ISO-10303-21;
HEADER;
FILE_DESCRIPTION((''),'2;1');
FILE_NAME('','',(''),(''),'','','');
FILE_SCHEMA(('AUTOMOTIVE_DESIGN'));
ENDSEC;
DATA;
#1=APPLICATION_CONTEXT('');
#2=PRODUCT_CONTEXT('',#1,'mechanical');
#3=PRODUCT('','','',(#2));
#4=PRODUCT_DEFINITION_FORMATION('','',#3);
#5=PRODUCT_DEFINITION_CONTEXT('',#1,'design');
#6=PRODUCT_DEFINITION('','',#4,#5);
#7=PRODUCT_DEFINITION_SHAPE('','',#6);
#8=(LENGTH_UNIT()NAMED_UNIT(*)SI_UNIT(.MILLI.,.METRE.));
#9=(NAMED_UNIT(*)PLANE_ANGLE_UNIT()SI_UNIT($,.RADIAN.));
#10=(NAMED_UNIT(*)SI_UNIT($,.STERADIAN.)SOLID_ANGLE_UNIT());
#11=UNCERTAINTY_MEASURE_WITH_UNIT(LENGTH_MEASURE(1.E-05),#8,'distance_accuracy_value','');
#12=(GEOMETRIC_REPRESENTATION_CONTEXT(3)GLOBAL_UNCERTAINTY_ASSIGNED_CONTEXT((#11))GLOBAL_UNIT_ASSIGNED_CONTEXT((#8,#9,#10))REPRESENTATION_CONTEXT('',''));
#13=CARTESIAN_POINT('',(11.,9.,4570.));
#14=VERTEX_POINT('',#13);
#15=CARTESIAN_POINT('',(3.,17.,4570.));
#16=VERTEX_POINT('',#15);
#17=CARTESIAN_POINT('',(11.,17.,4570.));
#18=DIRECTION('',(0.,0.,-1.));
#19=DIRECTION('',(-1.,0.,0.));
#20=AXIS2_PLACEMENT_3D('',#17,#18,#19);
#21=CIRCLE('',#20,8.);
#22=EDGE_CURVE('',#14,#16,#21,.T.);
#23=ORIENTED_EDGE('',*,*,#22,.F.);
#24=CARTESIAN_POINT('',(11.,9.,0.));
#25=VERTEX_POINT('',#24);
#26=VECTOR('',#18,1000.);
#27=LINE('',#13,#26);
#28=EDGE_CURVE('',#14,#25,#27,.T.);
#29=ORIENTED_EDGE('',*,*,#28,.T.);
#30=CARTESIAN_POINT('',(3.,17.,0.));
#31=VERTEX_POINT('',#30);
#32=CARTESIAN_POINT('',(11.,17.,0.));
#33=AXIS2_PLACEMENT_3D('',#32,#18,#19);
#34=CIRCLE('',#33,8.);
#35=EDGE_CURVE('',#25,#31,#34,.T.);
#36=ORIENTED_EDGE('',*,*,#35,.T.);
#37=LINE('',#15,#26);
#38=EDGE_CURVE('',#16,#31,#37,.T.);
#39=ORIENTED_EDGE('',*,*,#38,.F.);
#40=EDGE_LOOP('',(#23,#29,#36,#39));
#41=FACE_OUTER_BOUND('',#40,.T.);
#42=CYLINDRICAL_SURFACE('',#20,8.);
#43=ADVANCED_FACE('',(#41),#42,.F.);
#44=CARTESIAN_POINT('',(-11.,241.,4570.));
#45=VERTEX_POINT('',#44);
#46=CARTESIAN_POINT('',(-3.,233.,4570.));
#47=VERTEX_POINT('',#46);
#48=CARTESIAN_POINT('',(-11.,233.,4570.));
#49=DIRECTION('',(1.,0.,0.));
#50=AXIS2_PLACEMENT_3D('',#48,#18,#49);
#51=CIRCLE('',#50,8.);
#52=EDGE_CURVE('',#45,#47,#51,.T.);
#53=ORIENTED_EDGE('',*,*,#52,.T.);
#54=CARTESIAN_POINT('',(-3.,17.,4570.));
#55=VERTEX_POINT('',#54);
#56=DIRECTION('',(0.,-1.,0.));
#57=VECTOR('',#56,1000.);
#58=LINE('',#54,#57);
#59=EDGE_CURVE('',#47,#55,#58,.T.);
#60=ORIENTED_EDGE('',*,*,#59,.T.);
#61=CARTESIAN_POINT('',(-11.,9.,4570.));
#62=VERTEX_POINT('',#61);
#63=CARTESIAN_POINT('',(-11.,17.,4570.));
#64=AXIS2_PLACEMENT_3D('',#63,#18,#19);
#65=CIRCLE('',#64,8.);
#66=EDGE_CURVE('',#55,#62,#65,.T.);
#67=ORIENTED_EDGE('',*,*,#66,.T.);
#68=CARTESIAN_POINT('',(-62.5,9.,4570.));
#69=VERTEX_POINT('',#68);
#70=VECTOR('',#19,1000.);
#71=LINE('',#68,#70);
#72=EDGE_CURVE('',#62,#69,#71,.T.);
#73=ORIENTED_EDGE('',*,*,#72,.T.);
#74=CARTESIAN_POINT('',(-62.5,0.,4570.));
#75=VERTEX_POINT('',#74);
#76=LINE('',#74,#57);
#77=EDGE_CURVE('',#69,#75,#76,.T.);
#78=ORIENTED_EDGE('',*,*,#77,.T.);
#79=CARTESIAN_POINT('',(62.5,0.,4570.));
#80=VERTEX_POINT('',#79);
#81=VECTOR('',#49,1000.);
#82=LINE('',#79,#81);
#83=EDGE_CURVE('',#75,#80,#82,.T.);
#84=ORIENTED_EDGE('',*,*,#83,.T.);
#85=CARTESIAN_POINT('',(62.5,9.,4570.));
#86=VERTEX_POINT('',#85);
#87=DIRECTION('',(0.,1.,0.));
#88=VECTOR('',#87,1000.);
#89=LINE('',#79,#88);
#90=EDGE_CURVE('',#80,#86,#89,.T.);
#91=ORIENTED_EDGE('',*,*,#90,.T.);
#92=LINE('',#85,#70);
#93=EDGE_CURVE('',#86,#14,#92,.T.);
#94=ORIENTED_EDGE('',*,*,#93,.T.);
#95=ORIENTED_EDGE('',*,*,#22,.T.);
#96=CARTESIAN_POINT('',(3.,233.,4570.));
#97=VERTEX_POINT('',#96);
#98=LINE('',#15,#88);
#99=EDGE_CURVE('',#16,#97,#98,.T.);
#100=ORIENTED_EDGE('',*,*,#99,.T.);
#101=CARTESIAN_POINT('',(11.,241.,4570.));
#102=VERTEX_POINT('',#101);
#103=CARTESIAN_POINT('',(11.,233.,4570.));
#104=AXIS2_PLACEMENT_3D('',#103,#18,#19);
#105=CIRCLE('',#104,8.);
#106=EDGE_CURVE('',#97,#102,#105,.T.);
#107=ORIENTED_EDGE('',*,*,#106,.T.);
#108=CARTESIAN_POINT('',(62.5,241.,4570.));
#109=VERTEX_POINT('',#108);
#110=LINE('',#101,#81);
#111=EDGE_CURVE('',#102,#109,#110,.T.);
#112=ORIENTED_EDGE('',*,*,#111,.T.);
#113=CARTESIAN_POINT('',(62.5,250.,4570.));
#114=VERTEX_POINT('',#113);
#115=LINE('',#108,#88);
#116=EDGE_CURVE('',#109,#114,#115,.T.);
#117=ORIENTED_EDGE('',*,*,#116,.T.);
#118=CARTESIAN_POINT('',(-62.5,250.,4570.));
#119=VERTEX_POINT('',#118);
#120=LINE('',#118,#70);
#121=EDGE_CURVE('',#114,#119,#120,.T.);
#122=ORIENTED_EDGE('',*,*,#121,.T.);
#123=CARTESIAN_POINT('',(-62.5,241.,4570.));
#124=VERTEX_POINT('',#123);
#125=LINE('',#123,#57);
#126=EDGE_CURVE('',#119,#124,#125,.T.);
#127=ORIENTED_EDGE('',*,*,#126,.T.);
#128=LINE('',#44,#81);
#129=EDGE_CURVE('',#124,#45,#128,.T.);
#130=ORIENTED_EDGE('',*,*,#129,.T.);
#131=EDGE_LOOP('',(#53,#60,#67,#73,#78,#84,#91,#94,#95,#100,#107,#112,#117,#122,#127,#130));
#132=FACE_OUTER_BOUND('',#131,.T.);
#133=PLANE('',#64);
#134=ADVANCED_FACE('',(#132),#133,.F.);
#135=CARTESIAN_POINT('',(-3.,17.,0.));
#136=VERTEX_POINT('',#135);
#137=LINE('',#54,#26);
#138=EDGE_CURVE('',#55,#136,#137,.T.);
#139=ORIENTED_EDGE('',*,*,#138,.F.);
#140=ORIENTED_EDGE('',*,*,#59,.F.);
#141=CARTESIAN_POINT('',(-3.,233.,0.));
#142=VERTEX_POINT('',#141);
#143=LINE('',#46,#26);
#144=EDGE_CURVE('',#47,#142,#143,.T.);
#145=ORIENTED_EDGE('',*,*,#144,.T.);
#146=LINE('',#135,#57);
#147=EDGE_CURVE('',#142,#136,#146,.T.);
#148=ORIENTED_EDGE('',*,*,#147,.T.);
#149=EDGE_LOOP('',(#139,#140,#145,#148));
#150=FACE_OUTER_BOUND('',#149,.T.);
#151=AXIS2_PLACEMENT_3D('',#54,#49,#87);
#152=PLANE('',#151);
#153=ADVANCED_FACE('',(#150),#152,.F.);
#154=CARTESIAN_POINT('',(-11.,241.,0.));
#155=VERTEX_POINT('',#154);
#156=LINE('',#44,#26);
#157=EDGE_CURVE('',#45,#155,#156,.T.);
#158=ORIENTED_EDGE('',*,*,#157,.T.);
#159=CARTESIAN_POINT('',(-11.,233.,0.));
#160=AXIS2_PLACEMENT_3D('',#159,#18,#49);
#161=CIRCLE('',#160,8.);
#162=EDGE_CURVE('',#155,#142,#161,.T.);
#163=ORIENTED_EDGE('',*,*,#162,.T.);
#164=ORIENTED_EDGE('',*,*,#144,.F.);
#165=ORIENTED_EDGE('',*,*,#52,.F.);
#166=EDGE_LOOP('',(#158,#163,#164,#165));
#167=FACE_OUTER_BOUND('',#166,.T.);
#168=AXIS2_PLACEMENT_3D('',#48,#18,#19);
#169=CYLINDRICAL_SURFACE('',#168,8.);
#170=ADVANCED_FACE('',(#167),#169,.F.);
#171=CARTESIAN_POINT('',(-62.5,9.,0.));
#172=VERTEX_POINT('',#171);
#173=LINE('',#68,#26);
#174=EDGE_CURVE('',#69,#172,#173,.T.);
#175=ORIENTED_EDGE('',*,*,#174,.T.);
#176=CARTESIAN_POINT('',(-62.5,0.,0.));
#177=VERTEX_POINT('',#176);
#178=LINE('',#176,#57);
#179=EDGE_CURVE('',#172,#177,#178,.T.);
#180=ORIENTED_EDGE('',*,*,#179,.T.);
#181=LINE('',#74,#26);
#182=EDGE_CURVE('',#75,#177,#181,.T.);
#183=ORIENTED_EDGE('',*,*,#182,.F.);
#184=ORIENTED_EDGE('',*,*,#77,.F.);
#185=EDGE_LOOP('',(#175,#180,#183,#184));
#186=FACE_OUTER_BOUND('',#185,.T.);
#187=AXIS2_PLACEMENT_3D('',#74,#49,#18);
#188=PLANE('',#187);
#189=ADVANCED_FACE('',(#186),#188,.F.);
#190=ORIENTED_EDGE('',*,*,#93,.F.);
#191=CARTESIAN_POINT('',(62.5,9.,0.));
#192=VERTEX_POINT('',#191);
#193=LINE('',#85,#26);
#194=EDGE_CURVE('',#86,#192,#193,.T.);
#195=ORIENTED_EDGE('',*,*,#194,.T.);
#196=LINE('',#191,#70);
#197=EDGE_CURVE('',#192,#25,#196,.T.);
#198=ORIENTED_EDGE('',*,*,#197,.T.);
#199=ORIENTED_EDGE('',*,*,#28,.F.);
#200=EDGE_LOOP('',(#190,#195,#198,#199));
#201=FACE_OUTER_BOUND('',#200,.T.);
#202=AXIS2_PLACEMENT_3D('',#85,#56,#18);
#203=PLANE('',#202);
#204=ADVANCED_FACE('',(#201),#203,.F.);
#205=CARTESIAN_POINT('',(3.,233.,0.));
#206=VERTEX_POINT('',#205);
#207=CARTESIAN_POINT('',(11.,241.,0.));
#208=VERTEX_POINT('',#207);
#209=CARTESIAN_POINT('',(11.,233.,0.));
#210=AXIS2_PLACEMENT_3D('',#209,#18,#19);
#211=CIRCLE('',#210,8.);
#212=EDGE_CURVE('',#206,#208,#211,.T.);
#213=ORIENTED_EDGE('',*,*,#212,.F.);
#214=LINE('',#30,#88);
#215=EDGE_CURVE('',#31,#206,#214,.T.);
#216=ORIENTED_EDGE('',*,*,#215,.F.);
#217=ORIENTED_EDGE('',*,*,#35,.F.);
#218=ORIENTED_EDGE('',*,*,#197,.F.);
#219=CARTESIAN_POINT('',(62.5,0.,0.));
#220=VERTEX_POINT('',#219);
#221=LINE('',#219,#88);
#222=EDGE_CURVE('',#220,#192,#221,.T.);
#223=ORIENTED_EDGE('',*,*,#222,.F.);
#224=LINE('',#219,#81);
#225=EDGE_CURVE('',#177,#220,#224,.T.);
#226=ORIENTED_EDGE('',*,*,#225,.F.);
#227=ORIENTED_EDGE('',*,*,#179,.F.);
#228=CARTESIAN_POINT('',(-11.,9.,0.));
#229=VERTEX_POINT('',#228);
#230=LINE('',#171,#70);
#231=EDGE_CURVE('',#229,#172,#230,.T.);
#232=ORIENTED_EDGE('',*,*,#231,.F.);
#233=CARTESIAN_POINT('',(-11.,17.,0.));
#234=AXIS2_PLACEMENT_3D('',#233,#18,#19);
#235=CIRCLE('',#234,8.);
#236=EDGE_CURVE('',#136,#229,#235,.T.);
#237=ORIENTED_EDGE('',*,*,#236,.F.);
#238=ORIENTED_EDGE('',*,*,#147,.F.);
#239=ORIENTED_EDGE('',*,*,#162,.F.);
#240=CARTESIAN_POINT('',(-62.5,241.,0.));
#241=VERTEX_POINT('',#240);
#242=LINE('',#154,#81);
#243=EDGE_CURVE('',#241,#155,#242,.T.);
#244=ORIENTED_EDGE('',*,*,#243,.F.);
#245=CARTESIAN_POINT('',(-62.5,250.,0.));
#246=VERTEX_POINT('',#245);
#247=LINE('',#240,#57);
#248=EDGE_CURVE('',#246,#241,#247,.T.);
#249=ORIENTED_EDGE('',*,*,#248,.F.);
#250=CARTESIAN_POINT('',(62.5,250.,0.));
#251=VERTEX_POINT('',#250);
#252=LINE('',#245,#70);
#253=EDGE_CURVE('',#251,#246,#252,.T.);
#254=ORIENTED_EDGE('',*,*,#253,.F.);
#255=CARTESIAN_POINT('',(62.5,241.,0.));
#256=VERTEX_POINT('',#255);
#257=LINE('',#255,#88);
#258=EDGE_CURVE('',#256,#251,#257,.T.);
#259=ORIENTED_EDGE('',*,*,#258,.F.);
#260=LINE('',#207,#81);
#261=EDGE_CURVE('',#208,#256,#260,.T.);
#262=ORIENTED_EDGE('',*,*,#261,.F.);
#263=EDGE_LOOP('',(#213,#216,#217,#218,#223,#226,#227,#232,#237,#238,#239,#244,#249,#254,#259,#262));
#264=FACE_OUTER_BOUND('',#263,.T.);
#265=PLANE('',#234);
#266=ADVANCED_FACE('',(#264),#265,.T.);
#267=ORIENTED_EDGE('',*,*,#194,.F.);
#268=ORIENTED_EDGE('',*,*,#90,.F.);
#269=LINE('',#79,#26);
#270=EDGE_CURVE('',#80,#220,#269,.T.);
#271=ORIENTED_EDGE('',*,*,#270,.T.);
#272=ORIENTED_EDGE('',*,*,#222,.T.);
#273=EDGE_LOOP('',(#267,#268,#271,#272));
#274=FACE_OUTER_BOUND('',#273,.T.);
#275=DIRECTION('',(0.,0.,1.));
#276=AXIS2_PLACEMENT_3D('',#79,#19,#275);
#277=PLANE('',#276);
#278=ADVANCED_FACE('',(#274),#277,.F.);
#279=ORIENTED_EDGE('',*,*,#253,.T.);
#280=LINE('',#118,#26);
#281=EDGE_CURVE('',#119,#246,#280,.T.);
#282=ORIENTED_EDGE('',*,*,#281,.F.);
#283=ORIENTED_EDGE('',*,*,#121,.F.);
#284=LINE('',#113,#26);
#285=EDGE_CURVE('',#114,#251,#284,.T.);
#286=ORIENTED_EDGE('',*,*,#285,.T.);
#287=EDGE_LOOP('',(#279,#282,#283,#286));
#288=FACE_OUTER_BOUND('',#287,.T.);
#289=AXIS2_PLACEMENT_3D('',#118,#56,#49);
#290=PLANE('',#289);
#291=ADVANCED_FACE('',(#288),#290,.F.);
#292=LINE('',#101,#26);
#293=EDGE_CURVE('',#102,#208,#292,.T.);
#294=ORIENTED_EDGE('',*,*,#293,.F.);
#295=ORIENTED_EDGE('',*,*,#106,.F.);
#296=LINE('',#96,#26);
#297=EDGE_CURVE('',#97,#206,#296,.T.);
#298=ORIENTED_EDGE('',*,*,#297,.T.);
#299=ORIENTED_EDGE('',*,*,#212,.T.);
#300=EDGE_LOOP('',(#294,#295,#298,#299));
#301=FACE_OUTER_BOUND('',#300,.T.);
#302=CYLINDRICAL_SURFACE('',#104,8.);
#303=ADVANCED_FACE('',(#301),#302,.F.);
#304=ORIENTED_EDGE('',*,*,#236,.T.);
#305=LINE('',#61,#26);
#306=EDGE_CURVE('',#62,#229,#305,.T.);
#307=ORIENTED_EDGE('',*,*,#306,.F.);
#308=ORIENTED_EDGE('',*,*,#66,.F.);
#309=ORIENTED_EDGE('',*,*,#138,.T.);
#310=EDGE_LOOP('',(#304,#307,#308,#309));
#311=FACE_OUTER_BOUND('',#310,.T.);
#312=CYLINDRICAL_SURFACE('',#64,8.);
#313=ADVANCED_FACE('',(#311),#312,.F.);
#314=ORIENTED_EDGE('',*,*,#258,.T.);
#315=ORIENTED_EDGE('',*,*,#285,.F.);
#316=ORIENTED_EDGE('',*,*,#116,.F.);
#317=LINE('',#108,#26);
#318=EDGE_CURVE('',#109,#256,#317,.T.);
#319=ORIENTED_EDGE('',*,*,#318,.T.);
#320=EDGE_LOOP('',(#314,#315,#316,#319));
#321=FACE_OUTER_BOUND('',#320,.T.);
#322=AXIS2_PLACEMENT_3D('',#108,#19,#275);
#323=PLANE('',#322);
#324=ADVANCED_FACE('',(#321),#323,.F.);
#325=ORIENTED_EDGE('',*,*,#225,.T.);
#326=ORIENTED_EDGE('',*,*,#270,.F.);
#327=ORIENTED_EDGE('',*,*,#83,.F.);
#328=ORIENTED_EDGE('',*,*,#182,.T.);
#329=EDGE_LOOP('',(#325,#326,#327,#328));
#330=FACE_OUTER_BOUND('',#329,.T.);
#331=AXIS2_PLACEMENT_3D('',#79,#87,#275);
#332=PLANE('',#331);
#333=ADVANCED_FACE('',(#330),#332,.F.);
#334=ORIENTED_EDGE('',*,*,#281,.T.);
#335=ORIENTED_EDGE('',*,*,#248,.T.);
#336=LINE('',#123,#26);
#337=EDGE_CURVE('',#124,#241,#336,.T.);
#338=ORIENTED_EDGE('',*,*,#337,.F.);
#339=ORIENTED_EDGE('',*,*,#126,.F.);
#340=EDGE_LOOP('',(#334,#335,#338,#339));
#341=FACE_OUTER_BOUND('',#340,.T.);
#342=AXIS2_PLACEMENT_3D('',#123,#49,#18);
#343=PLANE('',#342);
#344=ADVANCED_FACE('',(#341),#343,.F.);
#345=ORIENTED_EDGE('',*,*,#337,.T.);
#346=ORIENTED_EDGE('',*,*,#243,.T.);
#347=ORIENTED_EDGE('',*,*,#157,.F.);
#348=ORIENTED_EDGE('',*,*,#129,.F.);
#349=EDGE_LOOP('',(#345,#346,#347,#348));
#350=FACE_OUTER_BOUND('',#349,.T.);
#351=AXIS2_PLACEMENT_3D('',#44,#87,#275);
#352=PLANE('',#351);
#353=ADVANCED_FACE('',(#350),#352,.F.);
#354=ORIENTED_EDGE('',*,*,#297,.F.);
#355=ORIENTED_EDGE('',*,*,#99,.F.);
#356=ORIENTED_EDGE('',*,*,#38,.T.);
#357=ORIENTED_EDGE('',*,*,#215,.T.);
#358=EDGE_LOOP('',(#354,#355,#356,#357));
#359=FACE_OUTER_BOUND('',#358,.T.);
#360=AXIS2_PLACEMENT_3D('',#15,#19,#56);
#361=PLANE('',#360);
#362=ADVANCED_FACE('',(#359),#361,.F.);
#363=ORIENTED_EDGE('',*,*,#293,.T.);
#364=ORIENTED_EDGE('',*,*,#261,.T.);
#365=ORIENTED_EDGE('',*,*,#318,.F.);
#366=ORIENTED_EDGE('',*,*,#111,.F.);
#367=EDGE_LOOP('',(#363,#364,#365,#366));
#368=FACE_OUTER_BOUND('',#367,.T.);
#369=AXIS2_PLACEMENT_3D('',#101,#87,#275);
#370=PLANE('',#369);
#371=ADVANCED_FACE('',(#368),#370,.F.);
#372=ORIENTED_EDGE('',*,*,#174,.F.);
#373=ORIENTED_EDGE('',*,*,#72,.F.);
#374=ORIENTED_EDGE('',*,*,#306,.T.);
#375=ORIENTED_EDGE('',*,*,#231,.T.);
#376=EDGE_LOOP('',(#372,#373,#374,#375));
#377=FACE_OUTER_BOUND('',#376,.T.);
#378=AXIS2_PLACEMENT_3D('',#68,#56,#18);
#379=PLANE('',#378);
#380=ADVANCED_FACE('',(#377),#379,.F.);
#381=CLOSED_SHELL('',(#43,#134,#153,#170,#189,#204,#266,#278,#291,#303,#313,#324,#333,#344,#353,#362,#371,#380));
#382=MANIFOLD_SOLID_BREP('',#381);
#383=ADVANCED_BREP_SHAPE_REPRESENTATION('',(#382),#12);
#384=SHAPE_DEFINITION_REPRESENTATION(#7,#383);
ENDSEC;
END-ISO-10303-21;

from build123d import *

# Parameters (mm, degrees)
BOSS_EXTRUDE1_DEPTH = 4570


with BuildPart() as part:
    # Sketch1 → Boss-Extrude1 (new body)
    with BuildSketch(Plane.XY):
        with BuildLine():
            Line((62.5, 0), (-62.5, 0))
            Line((-62.5, 0), (-62.5, 9))
            Line((-62.5, 9), (-11, 9))
            ThreePointArc((-11, 9), (-5.343145751, 11.343145751), (-3, 17))
            Line((-3, 17), (-3, 233))
            ThreePointArc((-3, 233), (-5.343145751, 238.656854249), (-11, 241))
            Line((-11, 241), (-62.5, 241))
            Line((-62.5, 241), (-62.5, 250))
            Line((-62.5, 250), (62.5, 250))
            Line((62.5, 250), (62.5, 241))
            Line((62.5, 241), (11, 241))
            ThreePointArc((11, 241), (5.343145751, 238.656854249), (3, 233))
            Line((3, 233), (3, 17))
            ThreePointArc((3, 17), (5.343145751, 11.343145751), (11, 9))
            Line((11, 9), (62.5, 9))
            Line((62.5, 9), (62.5, 0))
        make_face()
    extrude(amount=BOSS_EXTRUDE1_DEPTH)


solid = part.part
